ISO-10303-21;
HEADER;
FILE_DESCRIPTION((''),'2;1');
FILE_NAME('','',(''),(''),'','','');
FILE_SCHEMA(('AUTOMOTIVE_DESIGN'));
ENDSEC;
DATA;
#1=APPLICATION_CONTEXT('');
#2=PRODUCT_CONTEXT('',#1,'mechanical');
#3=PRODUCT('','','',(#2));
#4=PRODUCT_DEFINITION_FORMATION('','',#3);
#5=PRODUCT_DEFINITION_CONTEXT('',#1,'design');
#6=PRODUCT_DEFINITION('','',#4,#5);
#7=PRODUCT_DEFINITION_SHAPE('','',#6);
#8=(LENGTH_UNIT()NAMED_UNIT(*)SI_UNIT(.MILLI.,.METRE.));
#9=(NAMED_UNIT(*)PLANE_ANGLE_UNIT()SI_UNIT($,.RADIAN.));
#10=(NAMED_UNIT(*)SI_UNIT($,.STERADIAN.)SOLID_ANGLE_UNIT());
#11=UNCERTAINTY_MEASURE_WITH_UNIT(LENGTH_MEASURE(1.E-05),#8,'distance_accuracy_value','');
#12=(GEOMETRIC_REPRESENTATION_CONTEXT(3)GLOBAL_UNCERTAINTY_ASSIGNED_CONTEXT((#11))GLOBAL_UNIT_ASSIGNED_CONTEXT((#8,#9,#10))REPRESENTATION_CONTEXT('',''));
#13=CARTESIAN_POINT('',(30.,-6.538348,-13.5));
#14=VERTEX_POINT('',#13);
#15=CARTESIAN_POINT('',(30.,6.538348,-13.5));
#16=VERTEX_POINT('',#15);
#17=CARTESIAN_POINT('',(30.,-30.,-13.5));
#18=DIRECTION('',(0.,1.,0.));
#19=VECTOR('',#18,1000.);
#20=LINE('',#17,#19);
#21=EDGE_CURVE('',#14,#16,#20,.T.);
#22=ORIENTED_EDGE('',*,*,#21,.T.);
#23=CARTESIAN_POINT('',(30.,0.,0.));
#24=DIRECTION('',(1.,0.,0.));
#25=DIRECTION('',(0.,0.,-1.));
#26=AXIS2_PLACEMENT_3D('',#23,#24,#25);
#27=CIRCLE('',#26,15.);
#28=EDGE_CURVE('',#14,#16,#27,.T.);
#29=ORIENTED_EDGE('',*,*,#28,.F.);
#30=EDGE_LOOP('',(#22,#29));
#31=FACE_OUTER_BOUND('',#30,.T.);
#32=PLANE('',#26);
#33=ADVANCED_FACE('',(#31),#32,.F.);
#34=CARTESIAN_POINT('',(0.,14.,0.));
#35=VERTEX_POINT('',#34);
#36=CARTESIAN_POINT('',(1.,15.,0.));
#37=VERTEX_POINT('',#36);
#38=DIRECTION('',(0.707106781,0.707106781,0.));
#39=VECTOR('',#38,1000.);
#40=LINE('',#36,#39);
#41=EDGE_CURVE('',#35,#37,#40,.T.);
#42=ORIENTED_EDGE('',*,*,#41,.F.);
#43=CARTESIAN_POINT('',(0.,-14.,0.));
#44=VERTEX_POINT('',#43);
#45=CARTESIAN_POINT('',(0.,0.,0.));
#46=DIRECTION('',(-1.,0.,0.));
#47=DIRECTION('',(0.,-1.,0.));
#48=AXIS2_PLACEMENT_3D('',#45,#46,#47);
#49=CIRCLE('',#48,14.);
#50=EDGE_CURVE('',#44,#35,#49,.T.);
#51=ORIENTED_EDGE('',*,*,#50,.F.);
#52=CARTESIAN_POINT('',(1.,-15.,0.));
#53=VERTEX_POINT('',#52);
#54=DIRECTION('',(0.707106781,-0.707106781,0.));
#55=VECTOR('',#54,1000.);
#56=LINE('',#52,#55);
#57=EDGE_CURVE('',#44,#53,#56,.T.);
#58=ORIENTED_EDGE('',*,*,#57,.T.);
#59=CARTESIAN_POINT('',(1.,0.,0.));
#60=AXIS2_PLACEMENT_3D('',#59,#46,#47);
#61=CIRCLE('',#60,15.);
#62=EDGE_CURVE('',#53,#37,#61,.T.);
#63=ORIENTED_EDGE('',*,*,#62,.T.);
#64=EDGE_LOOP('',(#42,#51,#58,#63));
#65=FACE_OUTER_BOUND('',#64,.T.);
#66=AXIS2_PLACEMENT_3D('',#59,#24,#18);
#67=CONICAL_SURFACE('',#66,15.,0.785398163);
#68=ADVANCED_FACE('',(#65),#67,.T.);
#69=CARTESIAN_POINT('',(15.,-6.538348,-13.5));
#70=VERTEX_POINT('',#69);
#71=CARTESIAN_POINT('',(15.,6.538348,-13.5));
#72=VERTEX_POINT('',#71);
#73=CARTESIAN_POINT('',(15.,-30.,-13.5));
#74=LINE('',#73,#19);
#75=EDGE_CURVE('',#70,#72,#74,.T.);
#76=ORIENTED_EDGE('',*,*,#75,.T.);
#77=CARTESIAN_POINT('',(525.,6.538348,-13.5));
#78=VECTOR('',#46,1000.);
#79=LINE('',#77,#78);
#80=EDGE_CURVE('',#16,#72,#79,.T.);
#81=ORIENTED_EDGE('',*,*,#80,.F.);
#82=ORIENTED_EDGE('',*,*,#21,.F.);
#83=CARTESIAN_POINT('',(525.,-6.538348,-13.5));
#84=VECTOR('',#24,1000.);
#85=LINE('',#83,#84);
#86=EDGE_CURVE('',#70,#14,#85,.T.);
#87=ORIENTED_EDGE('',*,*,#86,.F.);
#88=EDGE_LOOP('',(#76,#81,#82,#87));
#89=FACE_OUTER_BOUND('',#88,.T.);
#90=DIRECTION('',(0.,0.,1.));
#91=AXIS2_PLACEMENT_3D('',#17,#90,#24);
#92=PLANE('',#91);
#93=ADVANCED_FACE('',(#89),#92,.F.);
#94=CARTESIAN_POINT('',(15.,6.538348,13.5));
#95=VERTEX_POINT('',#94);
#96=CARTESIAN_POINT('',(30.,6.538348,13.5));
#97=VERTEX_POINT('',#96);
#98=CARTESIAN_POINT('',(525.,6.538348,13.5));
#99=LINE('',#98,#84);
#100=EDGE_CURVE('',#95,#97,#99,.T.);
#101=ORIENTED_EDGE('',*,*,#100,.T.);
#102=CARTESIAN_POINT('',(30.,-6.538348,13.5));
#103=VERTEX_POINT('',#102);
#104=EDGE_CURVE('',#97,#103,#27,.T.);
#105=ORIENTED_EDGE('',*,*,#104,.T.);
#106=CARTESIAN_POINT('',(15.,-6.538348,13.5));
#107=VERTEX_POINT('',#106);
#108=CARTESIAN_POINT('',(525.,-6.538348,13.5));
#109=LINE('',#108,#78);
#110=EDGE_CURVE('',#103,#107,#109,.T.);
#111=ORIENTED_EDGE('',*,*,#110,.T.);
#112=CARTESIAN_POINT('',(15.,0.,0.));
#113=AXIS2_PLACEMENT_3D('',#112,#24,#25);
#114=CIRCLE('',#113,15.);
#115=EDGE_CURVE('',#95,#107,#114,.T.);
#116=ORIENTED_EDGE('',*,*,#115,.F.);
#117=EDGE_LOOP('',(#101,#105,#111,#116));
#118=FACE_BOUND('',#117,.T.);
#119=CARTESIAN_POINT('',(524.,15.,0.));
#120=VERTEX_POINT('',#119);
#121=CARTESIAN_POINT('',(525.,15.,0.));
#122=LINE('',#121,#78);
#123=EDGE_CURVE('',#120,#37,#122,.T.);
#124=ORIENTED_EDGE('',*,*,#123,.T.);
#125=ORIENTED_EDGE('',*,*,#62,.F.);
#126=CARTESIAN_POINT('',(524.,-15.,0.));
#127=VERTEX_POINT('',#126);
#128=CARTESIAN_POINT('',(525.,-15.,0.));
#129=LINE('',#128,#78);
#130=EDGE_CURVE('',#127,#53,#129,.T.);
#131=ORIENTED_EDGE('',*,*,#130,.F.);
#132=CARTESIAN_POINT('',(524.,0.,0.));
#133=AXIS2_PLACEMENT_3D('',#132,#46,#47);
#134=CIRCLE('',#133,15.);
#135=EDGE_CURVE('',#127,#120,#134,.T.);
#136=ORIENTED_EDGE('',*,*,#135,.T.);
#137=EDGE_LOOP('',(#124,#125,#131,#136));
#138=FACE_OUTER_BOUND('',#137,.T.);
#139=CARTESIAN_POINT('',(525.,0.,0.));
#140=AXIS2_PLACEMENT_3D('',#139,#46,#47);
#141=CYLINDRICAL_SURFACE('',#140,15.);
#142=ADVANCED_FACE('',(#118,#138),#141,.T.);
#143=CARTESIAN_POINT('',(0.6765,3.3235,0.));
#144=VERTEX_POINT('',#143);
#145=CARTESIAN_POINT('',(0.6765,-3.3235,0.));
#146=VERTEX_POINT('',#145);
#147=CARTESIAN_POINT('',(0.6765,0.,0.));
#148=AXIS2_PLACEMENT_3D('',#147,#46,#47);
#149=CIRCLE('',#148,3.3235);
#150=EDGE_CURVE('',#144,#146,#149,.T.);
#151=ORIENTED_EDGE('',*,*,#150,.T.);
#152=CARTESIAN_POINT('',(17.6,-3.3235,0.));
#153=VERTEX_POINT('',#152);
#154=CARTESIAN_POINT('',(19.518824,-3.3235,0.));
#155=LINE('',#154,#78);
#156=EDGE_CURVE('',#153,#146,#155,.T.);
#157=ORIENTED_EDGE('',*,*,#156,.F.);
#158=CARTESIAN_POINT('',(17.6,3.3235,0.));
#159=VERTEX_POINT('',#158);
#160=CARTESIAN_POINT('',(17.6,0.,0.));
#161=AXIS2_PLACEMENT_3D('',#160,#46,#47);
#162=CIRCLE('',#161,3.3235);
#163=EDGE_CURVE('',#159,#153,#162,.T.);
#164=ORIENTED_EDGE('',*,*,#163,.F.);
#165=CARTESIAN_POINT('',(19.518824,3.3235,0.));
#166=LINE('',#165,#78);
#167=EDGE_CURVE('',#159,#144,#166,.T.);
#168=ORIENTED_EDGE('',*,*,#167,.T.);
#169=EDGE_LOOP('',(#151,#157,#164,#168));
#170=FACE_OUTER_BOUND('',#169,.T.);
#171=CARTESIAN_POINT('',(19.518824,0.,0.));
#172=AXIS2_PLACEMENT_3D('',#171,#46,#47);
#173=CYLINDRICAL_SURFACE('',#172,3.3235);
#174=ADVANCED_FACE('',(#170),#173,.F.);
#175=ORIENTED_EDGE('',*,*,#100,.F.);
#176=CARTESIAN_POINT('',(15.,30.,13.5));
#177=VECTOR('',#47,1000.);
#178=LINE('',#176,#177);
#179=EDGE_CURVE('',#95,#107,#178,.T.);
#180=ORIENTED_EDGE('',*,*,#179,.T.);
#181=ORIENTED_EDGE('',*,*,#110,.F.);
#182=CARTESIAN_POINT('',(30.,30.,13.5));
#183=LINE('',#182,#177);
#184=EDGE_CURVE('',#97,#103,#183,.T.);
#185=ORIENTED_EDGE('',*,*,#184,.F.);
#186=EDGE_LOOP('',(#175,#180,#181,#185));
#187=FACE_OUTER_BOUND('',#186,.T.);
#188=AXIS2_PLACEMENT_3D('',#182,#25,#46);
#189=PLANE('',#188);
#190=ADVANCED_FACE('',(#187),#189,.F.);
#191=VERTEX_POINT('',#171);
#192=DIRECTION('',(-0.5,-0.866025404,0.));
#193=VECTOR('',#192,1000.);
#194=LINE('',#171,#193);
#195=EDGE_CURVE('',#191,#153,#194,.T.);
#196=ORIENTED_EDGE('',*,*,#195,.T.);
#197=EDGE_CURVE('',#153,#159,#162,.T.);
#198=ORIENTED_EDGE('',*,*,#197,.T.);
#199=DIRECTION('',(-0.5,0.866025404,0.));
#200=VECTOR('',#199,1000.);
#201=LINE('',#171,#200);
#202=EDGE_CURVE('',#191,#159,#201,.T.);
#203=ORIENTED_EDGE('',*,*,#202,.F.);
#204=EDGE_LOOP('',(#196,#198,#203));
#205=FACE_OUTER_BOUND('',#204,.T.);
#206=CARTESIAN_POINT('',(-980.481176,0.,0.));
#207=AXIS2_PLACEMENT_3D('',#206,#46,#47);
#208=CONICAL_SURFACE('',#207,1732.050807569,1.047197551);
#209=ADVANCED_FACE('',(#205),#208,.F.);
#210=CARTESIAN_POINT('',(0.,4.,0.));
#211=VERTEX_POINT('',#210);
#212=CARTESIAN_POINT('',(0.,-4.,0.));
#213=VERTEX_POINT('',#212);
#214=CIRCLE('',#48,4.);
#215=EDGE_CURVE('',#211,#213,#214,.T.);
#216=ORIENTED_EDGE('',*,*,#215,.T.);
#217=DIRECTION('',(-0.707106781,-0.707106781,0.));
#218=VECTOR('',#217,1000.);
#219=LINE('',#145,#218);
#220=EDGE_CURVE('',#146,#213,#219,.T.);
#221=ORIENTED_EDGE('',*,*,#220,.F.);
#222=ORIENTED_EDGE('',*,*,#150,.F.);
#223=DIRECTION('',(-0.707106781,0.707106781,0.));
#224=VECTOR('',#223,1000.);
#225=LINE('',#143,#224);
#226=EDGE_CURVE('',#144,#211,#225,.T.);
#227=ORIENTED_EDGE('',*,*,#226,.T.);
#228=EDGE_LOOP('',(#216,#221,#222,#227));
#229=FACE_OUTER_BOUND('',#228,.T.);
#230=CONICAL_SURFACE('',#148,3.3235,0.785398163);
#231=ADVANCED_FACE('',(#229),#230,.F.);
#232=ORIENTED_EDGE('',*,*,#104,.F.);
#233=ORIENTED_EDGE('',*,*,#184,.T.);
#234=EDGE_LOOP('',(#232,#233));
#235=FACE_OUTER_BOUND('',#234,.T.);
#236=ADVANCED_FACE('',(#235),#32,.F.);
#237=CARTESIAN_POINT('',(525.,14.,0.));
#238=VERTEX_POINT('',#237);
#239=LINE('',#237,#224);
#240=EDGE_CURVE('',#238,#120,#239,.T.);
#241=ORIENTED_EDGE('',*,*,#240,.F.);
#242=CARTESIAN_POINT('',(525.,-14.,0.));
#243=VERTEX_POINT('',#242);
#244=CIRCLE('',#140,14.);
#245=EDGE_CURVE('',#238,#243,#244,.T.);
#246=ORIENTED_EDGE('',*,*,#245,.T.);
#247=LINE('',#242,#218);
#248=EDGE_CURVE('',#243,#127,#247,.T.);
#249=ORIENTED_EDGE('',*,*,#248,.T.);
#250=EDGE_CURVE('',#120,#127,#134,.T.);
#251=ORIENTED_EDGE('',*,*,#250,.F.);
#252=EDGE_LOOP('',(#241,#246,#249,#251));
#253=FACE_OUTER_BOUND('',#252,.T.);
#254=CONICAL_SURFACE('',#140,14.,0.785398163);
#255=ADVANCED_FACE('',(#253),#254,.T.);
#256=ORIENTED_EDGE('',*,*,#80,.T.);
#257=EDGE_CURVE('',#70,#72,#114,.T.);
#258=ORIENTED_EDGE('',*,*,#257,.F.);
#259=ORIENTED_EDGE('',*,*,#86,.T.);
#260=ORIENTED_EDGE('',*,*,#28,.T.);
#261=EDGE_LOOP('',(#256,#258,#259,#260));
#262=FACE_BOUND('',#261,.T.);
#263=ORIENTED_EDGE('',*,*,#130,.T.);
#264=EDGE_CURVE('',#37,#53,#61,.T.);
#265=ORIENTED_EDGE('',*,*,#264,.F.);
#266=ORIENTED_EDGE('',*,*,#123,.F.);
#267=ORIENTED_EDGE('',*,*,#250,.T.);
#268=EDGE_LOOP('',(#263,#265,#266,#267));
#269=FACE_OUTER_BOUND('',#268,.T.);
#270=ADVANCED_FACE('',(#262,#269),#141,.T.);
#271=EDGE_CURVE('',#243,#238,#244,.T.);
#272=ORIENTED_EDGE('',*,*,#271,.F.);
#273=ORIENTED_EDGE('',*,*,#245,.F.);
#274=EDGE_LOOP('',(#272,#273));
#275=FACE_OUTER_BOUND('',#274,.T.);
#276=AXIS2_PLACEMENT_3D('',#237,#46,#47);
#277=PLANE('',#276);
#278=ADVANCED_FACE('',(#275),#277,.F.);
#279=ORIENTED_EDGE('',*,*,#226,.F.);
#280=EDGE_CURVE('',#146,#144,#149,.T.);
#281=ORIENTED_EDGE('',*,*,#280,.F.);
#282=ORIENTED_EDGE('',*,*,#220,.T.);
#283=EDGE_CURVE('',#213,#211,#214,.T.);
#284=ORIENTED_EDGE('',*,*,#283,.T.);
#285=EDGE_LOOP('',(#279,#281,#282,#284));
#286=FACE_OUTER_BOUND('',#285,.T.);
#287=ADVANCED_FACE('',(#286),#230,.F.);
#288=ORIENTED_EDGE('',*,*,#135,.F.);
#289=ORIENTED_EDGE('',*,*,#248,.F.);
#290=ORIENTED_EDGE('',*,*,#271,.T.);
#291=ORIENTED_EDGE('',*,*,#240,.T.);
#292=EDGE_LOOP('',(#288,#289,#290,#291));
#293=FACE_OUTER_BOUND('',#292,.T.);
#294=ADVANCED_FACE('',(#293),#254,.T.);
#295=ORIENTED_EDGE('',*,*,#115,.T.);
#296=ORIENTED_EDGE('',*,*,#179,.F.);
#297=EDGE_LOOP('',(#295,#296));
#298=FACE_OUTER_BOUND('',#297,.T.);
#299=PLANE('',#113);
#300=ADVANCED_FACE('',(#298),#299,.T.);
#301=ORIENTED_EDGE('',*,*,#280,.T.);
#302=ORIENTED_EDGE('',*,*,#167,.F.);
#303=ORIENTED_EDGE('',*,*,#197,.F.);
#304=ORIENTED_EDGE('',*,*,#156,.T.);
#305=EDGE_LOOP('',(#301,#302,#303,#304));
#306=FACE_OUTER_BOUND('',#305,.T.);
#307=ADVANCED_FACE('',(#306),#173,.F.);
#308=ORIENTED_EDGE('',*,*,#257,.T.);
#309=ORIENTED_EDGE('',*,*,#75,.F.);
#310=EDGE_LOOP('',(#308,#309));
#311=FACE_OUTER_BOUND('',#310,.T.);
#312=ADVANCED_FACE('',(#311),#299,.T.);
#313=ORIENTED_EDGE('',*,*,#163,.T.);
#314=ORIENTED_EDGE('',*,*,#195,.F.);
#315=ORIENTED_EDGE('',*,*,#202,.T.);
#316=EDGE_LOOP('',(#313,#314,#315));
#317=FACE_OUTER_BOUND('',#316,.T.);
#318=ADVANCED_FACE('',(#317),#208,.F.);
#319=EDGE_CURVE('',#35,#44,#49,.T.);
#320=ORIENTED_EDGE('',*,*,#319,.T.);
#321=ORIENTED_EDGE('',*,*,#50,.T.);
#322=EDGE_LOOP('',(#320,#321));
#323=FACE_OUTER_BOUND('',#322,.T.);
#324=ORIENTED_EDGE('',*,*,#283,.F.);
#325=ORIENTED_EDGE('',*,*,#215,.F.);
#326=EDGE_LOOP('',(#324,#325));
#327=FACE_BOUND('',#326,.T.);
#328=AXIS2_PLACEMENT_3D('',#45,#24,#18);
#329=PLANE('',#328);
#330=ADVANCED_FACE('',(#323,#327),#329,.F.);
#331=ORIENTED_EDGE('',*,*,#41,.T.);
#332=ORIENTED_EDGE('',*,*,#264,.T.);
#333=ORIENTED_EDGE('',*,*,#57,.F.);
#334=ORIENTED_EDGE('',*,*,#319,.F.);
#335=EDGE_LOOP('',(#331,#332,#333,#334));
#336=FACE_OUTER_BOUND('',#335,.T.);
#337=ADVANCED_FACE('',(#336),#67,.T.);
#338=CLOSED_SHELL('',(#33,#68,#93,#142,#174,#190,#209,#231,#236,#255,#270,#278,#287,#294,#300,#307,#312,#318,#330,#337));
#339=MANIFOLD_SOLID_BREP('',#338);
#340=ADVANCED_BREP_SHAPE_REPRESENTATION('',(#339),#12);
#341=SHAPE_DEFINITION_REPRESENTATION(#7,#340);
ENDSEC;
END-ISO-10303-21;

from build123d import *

# Parameters (mm, degrees)
SKETCH3_W          = 54
SKETCH3_H          = 120
SKETCH3_W_2        = 27
SKETCH3_H_2        = 60
CUT_EXTRUDE1_DEPTH = 15


with BuildPart() as part:
    # Sketch1 → Revolve1 (revolve)
    with BuildSketch(Plane.XY, mode=Mode.PRIVATE) as revolve1_sk:
        Polygon((0, 0), (0, 14), (1, 15), (524, 15), (525, 14), (525, 0), align=None)
    revolve(revolve1_sk.sketch.rotate(Axis((525, 0, 0), (-1, 0, 0)), 180), axis=Axis((525, 0, 0), (-1, 0, 0)))

    # Sketch2 → Cut-Revolve1 (revolve, cut)
    with BuildSketch(Plane.XY, mode=Mode.PRIVATE) as cut_revolve1_sk:
        Polygon((0, 0), (0, 4), (0.6765, 3.3235), (17.6, 3.3235), (19.51882362, 0), align=None)
    revolve(cut_revolve1_sk.sketch.rotate(Axis((19.51882362, 0, 0), (-1, 0, 0)), 180), axis=Axis((19.51882362, 0, 0), (-1, 0, 0)), mode=Mode.SUBTRACT)

    # Sketch3 → Cut-Extrude1 (cut)
    with BuildSketch(Plane(origin=(15, 0, 0), x_dir=(0, 0, -1), z_dir=(1, 0, 0))):
        Rectangle(SKETCH3_W, SKETCH3_H)
        Rectangle(SKETCH3_W_2, SKETCH3_H_2, mode=Mode.SUBTRACT)
    extrude(amount=CUT_EXTRUDE1_DEPTH, mode=Mode.SUBTRACT)


solid = part.part
